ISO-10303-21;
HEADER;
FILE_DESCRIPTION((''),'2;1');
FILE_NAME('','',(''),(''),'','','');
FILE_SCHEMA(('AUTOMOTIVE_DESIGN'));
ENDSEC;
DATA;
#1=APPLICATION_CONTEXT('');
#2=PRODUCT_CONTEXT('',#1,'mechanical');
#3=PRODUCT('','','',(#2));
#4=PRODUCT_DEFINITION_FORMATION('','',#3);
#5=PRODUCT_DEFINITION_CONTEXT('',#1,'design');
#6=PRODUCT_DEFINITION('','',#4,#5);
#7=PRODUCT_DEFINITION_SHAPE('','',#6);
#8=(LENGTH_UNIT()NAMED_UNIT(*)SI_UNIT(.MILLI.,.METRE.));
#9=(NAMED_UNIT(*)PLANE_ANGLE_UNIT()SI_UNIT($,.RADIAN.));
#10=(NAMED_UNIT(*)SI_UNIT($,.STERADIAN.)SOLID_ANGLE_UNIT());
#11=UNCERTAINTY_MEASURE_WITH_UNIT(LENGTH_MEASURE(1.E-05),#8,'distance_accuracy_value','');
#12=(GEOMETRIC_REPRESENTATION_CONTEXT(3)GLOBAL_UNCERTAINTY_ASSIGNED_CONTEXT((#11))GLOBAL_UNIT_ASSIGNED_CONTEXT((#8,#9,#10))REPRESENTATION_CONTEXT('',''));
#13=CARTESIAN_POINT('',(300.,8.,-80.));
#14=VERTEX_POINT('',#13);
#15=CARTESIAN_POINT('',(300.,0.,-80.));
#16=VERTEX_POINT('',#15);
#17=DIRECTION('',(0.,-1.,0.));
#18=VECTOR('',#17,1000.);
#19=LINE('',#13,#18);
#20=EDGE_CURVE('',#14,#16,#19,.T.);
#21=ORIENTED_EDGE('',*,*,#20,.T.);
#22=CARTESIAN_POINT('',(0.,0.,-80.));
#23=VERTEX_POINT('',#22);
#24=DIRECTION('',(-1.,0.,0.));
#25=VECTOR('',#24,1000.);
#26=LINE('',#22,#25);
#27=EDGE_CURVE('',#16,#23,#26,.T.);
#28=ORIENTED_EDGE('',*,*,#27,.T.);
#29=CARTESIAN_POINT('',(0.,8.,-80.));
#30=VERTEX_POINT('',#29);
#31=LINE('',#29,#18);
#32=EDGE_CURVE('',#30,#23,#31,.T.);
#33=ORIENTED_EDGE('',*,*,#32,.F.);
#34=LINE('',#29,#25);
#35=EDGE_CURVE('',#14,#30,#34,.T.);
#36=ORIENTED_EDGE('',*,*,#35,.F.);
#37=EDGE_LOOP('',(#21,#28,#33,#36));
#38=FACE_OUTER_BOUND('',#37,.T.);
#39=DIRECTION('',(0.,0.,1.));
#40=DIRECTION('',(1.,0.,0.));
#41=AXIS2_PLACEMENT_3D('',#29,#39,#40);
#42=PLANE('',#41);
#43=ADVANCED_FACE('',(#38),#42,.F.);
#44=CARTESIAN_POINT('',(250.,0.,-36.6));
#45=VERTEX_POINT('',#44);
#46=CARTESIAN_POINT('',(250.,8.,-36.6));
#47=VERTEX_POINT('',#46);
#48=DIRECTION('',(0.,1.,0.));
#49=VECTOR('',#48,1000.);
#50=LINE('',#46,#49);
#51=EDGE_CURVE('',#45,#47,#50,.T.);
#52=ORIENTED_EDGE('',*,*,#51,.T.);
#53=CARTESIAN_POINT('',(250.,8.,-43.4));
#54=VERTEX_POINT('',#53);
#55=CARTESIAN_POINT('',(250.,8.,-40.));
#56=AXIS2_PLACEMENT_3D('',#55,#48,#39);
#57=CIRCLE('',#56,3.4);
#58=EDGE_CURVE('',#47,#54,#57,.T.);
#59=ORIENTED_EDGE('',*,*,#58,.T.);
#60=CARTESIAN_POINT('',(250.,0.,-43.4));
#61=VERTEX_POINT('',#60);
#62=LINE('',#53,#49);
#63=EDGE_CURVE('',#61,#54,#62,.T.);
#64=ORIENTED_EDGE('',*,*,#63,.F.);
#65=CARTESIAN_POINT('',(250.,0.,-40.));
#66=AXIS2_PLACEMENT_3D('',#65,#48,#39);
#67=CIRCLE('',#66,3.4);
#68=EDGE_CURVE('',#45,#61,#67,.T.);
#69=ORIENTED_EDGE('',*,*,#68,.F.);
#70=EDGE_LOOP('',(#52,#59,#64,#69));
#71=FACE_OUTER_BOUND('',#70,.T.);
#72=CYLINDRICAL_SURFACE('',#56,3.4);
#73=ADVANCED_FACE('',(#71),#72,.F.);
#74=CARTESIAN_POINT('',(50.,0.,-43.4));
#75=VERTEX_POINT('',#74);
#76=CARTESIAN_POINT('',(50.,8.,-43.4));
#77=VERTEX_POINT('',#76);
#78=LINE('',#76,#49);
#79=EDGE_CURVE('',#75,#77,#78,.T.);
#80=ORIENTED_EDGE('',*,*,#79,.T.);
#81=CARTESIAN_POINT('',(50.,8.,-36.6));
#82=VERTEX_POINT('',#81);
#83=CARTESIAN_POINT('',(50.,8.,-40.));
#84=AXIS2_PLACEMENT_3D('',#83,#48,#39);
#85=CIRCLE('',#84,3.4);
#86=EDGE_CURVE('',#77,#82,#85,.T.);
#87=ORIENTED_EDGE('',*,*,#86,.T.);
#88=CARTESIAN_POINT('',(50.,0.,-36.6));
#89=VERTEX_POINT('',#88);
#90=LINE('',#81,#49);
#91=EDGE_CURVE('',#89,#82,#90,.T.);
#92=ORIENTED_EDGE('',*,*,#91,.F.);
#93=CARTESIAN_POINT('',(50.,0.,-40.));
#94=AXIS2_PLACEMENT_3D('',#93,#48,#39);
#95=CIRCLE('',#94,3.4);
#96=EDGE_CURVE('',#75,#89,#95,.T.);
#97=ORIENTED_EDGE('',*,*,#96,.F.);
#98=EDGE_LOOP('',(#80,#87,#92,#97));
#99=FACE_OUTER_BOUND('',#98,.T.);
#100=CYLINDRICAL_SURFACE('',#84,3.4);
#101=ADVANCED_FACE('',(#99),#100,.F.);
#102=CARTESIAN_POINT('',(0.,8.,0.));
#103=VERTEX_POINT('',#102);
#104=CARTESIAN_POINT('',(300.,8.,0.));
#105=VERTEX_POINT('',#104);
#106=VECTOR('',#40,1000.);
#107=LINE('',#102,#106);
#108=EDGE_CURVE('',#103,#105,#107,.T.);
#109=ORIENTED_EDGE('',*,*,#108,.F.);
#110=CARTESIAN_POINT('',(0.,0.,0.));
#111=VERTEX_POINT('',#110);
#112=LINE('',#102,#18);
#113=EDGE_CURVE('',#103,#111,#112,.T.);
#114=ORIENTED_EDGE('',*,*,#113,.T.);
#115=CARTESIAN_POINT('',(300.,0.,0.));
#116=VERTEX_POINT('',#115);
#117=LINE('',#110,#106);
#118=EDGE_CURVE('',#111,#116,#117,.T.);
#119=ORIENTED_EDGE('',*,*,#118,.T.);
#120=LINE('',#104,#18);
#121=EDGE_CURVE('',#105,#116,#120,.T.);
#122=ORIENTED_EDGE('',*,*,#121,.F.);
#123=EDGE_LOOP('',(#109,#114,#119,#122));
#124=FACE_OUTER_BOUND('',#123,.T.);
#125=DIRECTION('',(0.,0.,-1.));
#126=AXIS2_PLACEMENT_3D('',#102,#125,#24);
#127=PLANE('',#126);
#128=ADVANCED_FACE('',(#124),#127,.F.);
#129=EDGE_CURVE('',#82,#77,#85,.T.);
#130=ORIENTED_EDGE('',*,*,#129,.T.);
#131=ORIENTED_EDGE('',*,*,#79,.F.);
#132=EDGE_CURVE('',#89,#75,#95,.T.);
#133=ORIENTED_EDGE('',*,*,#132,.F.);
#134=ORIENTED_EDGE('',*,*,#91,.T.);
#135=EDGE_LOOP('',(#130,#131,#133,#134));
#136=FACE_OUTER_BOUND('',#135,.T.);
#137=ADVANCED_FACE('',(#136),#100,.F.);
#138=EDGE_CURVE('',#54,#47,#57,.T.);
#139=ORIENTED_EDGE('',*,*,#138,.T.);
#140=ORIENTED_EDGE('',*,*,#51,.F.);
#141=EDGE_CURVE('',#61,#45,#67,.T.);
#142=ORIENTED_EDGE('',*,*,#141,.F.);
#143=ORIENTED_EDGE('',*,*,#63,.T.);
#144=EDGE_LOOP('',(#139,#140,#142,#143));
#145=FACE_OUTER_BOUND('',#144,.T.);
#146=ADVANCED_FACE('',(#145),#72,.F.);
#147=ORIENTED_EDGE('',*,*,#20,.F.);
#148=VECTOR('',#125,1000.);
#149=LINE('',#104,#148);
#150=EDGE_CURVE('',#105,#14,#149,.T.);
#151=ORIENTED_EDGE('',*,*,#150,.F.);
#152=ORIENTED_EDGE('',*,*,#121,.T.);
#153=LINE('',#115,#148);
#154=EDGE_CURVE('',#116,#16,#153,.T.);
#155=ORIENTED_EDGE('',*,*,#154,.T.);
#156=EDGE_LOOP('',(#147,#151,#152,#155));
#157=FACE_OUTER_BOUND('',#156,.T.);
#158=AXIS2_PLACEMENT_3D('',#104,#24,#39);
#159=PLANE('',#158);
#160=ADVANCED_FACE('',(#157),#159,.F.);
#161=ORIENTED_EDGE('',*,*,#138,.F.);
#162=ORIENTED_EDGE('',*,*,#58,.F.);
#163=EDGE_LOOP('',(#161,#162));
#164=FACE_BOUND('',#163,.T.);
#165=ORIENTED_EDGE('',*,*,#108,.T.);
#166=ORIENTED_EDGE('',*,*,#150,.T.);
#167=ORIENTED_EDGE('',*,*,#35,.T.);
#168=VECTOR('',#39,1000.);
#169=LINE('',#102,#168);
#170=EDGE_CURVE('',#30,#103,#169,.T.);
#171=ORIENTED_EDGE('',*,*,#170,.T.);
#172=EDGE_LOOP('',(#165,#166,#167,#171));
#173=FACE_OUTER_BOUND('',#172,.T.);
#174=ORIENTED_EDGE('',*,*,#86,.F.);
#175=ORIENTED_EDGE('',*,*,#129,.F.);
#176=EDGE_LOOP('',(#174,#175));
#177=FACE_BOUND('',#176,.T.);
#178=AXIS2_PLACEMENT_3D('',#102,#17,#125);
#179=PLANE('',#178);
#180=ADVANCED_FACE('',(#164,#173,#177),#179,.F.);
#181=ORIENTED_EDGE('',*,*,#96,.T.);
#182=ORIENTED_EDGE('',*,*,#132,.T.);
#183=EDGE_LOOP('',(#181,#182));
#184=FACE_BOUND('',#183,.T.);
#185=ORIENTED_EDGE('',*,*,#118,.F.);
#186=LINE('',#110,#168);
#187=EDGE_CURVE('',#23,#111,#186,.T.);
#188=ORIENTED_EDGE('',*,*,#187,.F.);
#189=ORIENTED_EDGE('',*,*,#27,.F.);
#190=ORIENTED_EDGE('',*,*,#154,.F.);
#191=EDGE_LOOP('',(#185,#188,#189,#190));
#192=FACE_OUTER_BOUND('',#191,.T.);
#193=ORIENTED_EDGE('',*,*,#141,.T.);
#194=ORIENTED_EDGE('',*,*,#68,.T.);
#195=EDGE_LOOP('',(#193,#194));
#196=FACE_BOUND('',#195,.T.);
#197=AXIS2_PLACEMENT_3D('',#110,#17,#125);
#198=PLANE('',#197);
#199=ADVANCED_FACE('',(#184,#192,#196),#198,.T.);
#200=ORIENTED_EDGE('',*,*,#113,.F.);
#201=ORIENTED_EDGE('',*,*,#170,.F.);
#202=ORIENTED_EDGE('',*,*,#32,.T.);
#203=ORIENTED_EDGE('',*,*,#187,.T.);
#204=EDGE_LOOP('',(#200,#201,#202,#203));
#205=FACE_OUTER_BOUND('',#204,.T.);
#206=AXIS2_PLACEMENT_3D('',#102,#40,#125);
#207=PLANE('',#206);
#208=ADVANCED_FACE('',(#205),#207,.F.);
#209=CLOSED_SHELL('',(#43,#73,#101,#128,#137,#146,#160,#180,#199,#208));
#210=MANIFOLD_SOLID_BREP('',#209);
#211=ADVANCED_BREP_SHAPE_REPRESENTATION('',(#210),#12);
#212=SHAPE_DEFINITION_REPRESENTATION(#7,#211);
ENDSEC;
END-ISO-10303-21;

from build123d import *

# Parameters (mm, degrees)
SKETCH1_W           = 300
SKETCH1_H           = 80
BOSS_EXTRUDE1_DEPTH = 8
M8_TAPPED_HOLE1_D   = 6.8


with BuildPart() as part:
    # Sketch1 → Boss-Extrude1 (new body)
    with BuildSketch(Plane(origin=(0, 0, 0), x_dir=(1, 0, 0), z_dir=(0, 1, 0))):
        with Locations((150, 40)):
            Rectangle(SKETCH1_W, SKETCH1_H)
    extrude(amount=BOSS_EXTRUDE1_DEPTH)

    # M8 Tapped Hole1 (through all)
    with Locations(Plane(origin=(0, 8, 0), x_dir=(1, 0, 0), z_dir=(0, 1, 0))):
        with Locations((50, 40), (250, 40)):
            Hole(M8_TAPPED_HOLE1_D / 2)


solid = part.part
